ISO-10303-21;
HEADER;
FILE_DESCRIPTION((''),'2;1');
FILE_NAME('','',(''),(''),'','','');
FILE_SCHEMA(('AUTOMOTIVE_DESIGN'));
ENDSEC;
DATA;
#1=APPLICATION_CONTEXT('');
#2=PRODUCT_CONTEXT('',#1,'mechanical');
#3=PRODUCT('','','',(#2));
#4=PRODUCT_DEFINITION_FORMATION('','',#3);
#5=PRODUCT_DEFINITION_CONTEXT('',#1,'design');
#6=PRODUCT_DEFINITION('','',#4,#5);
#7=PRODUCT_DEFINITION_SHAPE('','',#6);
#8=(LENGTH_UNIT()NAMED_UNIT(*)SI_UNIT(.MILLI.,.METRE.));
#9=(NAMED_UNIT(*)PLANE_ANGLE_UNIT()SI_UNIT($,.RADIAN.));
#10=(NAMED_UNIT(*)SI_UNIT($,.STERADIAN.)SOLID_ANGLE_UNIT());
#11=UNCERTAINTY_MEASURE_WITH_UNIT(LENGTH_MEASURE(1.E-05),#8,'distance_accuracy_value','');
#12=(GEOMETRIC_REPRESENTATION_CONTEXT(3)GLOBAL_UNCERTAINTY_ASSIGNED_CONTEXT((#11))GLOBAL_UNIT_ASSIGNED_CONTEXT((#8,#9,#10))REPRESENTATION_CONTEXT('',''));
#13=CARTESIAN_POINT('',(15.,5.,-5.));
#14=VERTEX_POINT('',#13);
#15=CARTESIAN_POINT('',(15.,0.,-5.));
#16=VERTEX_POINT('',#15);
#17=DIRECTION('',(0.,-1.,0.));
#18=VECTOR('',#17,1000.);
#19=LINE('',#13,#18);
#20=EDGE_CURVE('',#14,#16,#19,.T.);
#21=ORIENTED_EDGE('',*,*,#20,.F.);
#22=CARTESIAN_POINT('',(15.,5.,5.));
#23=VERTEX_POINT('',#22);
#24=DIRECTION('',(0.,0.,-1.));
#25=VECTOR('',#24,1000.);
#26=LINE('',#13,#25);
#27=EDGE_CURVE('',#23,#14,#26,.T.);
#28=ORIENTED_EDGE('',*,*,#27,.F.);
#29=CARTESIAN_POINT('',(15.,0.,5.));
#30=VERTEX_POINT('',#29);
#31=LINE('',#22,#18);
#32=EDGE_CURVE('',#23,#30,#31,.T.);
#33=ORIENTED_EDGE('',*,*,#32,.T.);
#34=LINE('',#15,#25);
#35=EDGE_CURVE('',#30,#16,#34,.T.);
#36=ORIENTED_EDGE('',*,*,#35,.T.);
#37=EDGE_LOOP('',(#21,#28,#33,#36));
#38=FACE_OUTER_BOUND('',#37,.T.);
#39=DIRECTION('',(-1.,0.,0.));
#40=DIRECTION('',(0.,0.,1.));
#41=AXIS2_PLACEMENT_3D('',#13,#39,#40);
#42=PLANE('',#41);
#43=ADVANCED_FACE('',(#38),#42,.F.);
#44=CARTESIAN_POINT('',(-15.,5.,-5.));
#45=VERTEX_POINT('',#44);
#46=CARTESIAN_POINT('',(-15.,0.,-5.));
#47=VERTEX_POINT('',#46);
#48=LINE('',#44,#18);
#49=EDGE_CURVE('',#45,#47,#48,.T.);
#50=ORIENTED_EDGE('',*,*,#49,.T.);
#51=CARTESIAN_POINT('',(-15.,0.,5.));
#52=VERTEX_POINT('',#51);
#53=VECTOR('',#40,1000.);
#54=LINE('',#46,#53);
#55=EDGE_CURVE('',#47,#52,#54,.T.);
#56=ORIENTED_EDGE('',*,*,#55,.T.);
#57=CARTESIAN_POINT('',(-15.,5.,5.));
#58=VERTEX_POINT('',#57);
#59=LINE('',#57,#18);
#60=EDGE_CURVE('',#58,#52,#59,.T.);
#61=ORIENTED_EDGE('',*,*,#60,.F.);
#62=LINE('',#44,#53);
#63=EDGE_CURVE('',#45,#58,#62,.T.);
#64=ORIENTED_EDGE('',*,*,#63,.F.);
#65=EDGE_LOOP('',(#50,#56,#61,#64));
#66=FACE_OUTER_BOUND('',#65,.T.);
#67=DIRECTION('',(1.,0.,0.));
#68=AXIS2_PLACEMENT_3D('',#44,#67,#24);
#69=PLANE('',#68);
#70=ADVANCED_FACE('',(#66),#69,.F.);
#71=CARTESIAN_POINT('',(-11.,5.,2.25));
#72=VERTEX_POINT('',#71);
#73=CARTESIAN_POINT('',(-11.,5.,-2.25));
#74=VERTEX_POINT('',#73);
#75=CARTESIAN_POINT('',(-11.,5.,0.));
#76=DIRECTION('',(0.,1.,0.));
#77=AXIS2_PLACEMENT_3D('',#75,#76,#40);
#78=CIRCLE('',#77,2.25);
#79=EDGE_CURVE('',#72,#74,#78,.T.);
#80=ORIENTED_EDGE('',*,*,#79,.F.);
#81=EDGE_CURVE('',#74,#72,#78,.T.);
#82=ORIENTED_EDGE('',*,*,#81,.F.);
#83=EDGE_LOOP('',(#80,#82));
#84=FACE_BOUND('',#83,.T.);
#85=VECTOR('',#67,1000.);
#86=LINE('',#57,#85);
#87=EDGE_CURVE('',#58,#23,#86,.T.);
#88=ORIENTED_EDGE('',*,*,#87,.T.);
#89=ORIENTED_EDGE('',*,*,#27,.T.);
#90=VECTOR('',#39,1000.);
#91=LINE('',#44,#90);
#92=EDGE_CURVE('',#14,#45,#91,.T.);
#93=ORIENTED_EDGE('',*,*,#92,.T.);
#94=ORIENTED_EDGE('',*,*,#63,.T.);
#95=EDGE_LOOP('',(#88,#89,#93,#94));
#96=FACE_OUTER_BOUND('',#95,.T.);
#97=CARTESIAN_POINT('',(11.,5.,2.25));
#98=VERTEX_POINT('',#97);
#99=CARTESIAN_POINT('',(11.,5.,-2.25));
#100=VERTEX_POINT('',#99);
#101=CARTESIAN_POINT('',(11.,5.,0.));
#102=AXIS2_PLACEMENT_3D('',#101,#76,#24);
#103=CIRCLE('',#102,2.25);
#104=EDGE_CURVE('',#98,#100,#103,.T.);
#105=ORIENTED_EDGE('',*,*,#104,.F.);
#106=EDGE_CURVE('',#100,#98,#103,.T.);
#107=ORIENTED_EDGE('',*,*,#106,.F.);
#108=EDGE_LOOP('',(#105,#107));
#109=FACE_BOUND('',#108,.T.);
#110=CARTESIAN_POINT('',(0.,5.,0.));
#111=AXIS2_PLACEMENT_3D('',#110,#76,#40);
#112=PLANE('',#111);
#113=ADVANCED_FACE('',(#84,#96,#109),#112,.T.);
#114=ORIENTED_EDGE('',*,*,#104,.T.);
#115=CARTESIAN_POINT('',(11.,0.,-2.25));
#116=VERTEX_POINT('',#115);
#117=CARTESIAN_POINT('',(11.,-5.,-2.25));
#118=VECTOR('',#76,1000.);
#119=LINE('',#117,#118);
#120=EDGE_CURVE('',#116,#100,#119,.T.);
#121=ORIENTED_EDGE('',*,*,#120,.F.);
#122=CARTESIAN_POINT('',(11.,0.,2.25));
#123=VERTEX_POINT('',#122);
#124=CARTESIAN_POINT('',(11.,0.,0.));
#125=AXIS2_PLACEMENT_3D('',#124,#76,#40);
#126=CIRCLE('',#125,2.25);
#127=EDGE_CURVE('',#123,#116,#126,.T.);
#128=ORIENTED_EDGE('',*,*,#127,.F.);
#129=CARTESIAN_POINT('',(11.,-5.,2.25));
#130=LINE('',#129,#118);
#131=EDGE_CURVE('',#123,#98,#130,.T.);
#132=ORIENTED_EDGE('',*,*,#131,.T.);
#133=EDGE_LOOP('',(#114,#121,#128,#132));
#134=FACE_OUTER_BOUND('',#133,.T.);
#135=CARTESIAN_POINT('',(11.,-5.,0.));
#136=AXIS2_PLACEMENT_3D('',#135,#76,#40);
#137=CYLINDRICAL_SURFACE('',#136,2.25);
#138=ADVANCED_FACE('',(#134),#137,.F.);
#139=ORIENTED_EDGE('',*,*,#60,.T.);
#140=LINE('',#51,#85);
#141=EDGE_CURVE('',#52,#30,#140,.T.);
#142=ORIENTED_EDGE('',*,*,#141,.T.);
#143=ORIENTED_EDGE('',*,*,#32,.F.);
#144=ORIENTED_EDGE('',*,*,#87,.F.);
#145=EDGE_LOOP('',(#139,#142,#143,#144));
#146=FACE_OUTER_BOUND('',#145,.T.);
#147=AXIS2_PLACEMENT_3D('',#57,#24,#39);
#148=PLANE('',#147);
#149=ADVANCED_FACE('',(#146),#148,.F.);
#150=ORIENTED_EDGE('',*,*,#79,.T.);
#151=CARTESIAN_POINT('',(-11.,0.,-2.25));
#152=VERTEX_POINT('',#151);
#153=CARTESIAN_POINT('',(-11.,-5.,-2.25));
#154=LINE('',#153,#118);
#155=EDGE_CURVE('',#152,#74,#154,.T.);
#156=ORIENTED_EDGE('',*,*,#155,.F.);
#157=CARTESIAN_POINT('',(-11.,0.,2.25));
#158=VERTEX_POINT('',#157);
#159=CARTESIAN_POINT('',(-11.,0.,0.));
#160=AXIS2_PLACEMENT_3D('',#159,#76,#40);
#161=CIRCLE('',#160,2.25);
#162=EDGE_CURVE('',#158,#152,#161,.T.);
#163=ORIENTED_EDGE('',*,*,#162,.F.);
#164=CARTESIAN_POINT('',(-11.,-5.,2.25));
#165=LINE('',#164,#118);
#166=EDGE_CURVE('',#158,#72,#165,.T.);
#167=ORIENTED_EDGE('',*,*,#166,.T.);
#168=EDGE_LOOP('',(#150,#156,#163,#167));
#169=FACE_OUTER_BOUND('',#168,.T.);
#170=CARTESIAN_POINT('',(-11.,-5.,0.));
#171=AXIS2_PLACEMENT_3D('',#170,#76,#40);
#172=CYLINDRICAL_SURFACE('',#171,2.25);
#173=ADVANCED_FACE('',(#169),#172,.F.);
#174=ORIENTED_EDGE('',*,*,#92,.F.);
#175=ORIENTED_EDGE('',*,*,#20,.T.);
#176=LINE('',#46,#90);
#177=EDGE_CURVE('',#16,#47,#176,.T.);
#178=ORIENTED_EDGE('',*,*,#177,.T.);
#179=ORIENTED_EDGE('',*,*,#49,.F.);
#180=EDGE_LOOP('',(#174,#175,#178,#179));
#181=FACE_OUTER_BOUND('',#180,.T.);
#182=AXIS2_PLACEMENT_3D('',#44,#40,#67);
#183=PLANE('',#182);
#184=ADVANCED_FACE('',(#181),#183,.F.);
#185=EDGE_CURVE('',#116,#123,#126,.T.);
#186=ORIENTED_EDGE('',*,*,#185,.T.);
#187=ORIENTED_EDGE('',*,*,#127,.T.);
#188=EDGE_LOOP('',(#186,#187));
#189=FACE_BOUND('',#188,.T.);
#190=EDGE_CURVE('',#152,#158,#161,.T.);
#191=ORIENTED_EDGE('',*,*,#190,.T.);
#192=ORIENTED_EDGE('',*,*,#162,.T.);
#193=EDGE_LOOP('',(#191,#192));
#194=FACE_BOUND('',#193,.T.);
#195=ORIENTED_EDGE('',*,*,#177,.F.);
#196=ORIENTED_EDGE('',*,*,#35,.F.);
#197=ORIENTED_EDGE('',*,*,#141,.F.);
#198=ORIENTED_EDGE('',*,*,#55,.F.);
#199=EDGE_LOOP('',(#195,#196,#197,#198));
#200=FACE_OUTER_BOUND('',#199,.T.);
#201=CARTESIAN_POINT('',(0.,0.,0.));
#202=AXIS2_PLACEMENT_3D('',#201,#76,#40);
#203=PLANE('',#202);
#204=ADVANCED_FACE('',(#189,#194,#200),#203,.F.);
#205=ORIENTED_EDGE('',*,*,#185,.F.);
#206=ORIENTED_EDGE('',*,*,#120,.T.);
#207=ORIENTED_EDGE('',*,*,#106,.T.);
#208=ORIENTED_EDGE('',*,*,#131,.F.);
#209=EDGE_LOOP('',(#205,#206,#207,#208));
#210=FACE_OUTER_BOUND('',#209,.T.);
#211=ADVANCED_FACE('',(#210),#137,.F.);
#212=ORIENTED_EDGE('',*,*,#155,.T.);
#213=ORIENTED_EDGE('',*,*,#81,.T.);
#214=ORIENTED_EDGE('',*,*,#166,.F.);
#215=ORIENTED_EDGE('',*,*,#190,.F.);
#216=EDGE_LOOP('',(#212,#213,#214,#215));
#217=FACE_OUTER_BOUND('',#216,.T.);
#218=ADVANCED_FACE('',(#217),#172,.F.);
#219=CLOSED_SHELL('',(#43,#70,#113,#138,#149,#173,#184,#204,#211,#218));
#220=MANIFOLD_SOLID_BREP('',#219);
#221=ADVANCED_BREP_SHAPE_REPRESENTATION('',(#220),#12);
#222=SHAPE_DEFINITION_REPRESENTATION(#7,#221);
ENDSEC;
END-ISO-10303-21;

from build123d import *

# Parameters (mm, degrees)
SKETCH1_W           = 30
SKETCH1_H           = 10
BOSS_EXTRUDE1_DEPTH = 5
SKETCH2_R           = 2.25
CUT_EXTRUDE1_DEPTH  = 10


with BuildPart() as part:
    # Sketch1 → Boss-Extrude1 (new body)
    with BuildSketch(Plane(origin=(0, 0, 0), x_dir=(1, 0, 0), z_dir=(0, 1, 0))):
        Rectangle(SKETCH1_W, SKETCH1_H)
    extrude(amount=BOSS_EXTRUDE1_DEPTH)

    # Sketch2 → Cut-Extrude1 (cut)
    with BuildSketch(Plane(origin=(0, 5, 0), x_dir=(1, 0, 0), z_dir=(0, 1, 0))):
        with Locations(Location((-11, 0, 0), (0, 0, 270))):
            Circle(SKETCH2_R)
        with Locations(Location((11, 0, 0), (0, 0, 270))):
            Circle(SKETCH2_R)
    extrude(amount=-CUT_EXTRUDE1_DEPTH, mode=Mode.SUBTRACT)


solid = part.part
